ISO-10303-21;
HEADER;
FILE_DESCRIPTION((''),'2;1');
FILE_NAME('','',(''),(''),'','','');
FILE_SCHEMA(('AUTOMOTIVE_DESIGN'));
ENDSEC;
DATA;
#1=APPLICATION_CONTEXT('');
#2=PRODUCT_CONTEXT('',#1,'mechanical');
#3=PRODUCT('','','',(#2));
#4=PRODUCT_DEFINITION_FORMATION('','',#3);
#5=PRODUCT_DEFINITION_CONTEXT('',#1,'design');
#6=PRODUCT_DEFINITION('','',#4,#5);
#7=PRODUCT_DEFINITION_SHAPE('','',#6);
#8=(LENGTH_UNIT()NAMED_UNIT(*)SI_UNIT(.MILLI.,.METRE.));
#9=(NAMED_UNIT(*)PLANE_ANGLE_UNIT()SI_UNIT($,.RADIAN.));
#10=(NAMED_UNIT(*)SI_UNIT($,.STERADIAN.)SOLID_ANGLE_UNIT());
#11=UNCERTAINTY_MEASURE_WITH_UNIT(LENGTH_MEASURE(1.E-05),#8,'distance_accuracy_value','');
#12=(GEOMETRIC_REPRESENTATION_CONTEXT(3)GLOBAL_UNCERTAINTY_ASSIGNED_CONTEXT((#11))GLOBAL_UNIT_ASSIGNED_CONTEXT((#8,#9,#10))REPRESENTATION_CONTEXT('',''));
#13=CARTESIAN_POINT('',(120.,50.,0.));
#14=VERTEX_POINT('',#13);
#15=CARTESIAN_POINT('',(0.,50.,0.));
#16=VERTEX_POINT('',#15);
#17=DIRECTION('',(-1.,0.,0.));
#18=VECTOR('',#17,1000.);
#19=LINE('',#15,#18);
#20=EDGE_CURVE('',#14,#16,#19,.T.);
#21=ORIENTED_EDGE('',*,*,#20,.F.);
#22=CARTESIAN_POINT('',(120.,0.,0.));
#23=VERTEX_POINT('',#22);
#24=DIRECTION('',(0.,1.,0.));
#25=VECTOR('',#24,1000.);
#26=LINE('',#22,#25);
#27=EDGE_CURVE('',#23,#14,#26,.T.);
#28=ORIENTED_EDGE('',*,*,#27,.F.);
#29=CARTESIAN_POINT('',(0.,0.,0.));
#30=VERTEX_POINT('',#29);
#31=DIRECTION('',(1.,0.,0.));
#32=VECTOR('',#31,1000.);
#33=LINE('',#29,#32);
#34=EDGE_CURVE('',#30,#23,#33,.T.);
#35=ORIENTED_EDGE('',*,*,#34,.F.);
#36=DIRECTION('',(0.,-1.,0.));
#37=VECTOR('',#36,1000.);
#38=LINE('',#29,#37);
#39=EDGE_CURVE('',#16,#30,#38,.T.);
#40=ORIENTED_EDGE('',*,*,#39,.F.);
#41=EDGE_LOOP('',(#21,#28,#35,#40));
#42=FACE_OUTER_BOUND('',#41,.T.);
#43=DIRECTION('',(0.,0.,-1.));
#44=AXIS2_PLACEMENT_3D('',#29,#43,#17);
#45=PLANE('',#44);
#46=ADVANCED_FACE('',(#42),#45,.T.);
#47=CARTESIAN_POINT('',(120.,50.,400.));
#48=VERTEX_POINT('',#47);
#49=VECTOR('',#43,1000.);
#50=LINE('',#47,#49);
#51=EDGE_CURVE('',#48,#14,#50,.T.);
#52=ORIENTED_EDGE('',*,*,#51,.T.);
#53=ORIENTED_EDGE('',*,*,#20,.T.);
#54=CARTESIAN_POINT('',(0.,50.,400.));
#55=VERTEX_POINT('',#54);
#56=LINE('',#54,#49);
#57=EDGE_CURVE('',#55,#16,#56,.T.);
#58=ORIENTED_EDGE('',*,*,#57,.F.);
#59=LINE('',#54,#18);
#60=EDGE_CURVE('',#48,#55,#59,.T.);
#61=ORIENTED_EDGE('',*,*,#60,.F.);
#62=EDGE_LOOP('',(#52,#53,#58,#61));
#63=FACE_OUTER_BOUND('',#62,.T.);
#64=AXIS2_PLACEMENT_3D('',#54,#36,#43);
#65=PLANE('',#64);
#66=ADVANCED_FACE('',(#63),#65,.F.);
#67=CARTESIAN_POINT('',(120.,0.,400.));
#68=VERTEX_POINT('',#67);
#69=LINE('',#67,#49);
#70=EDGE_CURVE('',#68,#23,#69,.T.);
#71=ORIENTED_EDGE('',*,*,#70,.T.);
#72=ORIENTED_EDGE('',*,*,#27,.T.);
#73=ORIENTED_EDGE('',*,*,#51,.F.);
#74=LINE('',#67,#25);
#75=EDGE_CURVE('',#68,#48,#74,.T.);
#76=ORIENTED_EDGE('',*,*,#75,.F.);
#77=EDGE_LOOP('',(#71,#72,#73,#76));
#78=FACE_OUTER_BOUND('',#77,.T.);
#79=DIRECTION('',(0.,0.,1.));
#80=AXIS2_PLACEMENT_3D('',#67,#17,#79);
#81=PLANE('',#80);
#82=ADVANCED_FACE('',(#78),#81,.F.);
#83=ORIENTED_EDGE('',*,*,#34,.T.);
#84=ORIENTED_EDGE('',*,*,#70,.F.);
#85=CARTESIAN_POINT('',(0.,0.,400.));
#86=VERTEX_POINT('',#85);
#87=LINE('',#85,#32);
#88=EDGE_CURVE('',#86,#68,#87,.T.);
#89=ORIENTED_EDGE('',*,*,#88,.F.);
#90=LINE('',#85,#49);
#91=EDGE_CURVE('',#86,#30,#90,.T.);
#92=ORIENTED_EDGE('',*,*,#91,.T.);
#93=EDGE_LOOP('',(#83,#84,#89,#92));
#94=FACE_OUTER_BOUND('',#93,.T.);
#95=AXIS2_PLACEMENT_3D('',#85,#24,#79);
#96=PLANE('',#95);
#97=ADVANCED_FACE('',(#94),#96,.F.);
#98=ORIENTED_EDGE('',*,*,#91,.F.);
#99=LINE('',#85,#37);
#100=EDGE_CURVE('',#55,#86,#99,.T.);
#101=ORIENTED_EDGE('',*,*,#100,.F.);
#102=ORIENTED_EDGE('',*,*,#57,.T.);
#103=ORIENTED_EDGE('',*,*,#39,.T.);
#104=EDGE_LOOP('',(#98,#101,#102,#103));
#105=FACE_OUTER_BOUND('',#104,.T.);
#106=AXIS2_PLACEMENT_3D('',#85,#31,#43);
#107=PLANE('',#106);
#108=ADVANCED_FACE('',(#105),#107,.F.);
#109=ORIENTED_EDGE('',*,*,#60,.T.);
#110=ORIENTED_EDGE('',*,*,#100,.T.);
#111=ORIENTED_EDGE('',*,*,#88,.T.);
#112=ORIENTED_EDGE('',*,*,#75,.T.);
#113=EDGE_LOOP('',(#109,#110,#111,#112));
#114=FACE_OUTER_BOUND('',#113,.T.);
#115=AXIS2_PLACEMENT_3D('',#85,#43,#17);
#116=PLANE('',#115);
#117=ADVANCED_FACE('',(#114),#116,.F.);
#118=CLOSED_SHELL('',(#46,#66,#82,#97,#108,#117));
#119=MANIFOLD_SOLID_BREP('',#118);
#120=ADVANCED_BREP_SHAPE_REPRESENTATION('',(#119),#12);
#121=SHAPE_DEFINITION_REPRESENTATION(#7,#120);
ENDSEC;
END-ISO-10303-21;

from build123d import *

# Parameters (mm, degrees)
SKETCH1_W           = 120
SKETCH1_H           = 50
BOSS_EXTRUDE1_DEPTH = 400


with BuildPart() as part:
    # Sketch1 → Boss-Extrude1 (new body)
    with BuildSketch(Plane.XY):
        with Locations((60, 25)):
            Rectangle(SKETCH1_W, SKETCH1_H)
    extrude(amount=BOSS_EXTRUDE1_DEPTH)


solid = part.part
